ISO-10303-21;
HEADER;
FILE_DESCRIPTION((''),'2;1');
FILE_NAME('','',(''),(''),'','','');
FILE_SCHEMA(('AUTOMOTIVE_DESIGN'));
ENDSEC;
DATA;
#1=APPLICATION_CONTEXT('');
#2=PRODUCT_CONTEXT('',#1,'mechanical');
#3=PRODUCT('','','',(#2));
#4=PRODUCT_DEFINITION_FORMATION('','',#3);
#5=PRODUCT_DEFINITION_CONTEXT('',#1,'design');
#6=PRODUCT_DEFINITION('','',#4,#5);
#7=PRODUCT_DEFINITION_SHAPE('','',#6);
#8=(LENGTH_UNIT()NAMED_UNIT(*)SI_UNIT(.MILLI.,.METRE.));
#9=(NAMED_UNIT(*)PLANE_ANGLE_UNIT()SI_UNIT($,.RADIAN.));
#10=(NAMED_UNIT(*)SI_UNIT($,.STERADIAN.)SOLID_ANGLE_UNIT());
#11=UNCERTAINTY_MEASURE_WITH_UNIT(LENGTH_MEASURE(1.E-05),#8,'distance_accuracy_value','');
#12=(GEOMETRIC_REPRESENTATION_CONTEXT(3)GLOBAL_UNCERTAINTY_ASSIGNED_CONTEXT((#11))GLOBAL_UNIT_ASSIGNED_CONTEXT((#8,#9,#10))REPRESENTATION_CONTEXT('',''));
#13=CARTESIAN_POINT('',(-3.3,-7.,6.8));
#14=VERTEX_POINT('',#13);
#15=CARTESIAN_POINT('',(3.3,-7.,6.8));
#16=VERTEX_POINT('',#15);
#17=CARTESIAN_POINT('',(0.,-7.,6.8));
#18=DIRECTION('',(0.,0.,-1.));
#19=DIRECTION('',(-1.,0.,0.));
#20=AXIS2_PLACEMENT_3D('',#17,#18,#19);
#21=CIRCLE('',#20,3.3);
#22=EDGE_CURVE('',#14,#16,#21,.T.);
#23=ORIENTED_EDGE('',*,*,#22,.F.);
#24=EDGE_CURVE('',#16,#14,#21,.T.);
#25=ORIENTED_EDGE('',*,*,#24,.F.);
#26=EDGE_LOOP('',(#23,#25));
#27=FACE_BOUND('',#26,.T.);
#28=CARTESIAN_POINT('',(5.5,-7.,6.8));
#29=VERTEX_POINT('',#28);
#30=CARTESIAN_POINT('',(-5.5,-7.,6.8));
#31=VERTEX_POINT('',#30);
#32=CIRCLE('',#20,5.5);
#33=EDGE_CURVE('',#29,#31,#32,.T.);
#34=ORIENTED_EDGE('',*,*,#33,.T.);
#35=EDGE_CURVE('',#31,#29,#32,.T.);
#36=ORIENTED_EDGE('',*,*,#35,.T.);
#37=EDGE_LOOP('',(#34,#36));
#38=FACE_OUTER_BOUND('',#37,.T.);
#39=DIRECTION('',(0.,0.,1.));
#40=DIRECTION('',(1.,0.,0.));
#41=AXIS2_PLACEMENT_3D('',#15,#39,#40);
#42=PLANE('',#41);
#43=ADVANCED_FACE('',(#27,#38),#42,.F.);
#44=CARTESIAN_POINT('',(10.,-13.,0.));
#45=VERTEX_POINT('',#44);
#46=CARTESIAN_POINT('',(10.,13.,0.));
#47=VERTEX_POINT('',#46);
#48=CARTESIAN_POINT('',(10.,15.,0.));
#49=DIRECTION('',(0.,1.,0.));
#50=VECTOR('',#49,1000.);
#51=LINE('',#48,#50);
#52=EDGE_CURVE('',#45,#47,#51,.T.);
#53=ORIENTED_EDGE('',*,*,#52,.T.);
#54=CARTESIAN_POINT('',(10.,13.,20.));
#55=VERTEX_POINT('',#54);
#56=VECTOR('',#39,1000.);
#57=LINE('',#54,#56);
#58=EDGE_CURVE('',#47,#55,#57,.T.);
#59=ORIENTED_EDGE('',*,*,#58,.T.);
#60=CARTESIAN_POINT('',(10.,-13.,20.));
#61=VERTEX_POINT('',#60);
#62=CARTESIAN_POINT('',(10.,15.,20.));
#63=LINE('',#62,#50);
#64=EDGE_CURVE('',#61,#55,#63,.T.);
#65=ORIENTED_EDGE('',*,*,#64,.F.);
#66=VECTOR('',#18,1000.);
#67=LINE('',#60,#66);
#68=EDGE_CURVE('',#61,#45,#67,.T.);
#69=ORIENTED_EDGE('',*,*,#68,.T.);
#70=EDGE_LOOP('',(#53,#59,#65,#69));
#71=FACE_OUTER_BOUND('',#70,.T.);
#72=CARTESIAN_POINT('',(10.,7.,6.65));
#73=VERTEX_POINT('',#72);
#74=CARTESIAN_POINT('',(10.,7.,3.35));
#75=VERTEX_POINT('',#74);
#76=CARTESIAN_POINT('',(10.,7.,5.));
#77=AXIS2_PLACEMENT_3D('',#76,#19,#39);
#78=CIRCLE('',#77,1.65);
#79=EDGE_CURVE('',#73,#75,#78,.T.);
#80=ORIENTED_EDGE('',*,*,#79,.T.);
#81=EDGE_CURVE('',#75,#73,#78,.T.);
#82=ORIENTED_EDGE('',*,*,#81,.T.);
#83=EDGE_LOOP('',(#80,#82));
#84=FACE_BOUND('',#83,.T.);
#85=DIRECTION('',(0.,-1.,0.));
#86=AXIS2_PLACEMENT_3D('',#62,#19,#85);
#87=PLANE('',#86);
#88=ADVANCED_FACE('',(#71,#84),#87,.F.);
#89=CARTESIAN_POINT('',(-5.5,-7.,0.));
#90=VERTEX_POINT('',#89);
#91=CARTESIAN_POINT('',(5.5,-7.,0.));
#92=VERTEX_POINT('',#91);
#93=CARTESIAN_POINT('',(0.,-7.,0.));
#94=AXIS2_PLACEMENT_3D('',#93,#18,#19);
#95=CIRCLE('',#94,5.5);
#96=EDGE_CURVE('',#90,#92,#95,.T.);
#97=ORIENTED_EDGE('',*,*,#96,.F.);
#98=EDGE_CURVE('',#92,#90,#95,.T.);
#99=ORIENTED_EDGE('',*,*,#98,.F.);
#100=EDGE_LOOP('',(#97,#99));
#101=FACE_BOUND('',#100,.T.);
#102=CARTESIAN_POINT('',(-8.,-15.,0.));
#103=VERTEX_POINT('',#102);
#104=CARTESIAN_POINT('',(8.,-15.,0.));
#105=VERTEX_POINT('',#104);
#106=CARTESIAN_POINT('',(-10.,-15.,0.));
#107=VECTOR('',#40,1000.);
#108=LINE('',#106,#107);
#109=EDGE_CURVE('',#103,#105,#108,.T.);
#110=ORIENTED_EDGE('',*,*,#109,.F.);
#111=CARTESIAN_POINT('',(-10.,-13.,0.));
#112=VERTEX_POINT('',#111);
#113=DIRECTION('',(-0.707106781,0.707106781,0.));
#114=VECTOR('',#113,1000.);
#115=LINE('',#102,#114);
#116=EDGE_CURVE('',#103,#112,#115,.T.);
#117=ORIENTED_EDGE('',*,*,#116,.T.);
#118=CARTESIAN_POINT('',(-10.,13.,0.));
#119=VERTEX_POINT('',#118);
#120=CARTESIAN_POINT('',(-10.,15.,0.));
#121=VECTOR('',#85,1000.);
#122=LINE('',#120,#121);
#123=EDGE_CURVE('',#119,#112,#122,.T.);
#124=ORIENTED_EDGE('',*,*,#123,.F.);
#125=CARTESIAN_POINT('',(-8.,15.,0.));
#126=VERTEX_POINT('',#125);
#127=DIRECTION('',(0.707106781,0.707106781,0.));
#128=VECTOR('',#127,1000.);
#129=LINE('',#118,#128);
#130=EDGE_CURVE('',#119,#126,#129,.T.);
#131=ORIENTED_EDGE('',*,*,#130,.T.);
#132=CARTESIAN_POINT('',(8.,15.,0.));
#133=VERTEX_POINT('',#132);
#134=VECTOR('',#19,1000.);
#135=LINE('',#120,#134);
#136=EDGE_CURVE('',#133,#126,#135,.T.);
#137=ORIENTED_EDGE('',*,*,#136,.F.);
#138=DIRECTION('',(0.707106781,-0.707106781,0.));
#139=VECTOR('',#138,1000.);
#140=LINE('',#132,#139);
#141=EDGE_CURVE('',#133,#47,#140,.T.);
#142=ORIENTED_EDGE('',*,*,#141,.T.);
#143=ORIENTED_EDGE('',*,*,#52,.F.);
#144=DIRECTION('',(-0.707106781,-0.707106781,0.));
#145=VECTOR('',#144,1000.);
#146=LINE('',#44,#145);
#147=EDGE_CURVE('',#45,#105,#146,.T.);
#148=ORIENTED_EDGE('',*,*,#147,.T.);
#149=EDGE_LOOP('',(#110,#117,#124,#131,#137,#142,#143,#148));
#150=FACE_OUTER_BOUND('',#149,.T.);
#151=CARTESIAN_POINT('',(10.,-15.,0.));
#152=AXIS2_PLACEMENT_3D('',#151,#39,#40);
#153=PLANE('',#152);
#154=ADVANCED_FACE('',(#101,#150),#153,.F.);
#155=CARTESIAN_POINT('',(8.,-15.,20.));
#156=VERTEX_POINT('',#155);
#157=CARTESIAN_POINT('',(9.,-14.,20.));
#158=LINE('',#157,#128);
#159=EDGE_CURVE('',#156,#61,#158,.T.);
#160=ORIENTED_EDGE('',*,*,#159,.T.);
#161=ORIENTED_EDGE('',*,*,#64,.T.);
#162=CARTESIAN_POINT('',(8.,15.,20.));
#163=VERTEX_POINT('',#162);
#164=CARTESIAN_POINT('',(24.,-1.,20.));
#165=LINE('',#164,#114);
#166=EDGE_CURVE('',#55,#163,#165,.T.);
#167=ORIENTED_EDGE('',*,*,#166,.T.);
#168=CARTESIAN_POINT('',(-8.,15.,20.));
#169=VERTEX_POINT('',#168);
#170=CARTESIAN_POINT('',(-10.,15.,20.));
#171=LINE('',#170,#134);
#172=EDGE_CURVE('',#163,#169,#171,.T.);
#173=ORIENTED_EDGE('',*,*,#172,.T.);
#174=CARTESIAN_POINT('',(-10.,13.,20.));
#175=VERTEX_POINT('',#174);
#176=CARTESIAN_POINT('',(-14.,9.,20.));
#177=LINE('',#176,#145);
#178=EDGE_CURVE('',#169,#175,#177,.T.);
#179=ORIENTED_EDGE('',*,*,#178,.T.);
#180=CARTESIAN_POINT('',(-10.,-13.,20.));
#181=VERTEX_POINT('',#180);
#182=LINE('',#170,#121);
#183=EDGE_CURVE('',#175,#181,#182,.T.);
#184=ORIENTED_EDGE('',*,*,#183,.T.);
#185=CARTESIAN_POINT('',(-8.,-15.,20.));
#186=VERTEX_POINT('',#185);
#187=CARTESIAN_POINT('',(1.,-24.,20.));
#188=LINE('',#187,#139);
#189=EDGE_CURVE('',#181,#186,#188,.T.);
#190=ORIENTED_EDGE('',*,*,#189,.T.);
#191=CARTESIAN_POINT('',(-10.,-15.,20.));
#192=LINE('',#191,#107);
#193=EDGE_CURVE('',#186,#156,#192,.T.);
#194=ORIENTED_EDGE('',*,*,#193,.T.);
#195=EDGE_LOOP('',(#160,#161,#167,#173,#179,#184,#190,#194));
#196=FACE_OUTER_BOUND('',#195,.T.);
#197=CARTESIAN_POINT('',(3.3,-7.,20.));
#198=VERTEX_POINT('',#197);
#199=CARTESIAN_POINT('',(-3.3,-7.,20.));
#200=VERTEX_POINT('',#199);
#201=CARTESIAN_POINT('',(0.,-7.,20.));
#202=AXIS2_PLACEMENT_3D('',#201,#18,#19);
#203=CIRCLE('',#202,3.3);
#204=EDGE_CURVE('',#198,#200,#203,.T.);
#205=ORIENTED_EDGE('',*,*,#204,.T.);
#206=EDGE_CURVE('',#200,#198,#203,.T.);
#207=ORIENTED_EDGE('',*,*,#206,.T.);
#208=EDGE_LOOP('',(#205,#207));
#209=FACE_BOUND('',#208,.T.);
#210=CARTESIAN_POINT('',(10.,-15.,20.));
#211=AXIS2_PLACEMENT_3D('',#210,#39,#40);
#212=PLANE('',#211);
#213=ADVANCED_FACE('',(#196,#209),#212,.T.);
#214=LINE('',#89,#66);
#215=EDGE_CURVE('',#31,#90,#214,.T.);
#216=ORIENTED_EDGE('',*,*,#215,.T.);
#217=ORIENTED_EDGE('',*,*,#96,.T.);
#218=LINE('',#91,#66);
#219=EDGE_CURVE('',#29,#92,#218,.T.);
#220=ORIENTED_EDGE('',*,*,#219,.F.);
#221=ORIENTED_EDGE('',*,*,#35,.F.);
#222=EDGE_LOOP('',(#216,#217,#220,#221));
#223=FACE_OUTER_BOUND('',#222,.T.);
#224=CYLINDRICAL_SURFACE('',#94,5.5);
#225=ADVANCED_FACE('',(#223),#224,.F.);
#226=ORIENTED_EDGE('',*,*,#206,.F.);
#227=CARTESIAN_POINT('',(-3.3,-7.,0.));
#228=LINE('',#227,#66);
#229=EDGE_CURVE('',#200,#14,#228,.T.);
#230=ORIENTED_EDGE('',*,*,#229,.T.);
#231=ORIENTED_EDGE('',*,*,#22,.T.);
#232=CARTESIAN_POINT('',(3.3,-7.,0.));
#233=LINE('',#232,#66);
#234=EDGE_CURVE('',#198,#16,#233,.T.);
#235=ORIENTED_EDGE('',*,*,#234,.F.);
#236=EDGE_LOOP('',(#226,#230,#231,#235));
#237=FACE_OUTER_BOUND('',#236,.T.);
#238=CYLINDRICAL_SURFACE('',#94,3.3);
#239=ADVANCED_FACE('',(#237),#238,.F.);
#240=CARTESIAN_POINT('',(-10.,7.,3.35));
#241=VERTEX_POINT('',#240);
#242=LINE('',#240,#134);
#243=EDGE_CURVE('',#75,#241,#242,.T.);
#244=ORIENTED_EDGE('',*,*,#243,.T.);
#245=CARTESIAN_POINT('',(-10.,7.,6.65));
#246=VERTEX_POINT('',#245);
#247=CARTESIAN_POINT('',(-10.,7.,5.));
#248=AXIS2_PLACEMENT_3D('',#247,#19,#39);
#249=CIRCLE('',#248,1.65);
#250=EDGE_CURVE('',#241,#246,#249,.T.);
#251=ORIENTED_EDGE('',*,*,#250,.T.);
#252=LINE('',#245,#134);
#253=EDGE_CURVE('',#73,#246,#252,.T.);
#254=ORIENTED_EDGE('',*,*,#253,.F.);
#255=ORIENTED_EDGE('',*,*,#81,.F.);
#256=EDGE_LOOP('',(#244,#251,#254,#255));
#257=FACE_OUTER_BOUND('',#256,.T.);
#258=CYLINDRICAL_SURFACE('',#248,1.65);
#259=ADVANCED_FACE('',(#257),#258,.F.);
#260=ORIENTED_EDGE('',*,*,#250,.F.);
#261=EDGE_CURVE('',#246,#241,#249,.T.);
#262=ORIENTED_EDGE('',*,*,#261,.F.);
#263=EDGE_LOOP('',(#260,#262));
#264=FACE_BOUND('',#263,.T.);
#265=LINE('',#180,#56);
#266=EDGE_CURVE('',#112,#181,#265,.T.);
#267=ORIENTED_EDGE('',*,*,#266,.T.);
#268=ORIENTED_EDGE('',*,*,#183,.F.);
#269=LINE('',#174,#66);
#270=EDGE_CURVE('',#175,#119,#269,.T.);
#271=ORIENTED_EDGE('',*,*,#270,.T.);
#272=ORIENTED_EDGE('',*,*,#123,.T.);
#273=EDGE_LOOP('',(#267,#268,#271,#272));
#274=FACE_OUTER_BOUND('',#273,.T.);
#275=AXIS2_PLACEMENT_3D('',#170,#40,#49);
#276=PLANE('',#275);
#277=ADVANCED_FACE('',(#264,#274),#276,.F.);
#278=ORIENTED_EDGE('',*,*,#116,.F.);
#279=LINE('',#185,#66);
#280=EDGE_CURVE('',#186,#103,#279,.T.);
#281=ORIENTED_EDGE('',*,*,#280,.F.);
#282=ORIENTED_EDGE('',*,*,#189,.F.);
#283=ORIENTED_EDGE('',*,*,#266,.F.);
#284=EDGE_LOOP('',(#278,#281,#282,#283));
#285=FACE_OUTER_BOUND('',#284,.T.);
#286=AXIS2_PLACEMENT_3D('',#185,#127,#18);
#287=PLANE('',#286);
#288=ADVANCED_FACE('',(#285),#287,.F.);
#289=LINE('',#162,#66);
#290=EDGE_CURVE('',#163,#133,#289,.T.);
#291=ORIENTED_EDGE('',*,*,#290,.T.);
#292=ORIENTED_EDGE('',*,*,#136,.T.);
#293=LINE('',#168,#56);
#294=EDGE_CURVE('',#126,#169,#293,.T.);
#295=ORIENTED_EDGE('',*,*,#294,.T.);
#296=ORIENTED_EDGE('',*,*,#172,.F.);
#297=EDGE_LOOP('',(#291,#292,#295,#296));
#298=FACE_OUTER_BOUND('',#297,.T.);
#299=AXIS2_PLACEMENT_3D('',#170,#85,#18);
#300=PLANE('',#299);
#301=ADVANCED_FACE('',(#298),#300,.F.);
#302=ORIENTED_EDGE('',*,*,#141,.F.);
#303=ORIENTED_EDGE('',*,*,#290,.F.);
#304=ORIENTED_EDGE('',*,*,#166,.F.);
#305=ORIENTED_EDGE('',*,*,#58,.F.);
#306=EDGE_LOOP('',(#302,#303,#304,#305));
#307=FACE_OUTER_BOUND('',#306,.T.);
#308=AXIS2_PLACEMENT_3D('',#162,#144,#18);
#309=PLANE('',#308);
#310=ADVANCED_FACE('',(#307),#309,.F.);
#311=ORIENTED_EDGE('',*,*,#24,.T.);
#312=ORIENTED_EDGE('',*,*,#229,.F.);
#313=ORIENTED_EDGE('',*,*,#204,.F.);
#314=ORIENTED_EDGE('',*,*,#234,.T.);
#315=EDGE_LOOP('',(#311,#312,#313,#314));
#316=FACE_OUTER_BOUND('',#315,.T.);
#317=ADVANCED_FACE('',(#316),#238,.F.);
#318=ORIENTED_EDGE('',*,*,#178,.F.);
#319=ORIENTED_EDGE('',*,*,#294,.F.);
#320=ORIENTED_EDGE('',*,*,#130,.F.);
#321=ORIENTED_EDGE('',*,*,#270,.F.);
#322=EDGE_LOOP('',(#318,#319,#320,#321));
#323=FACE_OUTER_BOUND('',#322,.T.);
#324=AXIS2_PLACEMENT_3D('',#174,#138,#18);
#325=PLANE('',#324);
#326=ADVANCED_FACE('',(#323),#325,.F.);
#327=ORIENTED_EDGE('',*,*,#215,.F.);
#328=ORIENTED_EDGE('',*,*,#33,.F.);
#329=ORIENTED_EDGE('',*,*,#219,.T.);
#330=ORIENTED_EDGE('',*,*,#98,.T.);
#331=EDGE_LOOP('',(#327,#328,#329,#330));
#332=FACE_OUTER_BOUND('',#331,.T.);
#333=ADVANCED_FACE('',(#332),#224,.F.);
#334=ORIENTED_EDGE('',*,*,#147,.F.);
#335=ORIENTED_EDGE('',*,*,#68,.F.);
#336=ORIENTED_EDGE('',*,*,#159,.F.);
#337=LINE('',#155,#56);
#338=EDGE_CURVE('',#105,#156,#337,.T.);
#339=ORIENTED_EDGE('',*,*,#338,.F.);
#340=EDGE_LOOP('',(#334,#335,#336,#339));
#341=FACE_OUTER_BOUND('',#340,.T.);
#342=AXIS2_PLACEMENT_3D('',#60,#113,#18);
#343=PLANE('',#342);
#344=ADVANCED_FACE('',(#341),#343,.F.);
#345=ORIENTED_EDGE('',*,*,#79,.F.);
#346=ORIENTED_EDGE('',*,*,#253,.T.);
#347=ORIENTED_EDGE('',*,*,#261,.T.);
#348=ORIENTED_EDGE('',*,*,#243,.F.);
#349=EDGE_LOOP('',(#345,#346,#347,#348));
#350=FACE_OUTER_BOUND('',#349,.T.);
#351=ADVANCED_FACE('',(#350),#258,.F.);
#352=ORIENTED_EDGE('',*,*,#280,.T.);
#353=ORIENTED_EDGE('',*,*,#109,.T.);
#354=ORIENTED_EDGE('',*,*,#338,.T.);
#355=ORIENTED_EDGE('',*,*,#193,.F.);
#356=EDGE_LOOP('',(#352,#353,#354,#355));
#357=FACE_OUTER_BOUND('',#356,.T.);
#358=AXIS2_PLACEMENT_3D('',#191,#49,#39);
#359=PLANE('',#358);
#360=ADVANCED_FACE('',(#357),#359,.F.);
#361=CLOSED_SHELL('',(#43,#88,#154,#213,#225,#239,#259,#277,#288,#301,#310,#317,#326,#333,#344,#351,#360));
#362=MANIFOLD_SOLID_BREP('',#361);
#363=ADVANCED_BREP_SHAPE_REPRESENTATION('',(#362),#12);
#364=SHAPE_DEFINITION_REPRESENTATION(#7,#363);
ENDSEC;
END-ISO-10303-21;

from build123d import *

# Parameters (mm, degrees)
SKETCH_1_W                = 20
SKETCH_1_H                = 30
EXTRUDE_1_DEPTH           = 20
HOLE_WIZARD_1_D           = 6.6
HOLE_WIZARD_1_CBORE_D     = 11
HOLE_WIZARD_1_CBORE_DEPTH = 6.8
HOLE_WIZARD_M4_1_D        = 3.3
CHAMFER_1_SIZE            = 2


with BuildPart() as part:
    # 草图1 → 凸台-拉伸1 (new body)
    with BuildSketch(Plane.XY):
        Rectangle(SKETCH_1_W, SKETCH_1_H)
    extrude(amount=EXTRUDE_1_DEPTH)

    # 打孔尺寸根据内六角圆柱头螺钉的类型1 (through all)
    with Locations(Plane(origin=(3.133596483, 10.907898158, 0), x_dir=(1, 0, 0), z_dir=(0, 0, -1))):
        with Locations((-3.133596483, 17.907898158)):
            CounterBoreHole(HOLE_WIZARD_1_D / 2, HOLE_WIZARD_1_CBORE_D / 2, HOLE_WIZARD_1_CBORE_DEPTH)

    # M4 螺纹孔1 (through all)
    with Locations(Plane.ZY.offset(10)):
        with Locations((5, 7)):
            Hole(HOLE_WIZARD_M4_1_D / 2)

    # 倒角1
    chamfer_1_edges = [part.edges().sort_by_distance(p)[0] for p in [
        (10, -15, 10),
        (-10, -15, 10),
        (-10, 15, 10),
        (10, 15, 10),
    ]]
    chamfer(chamfer_1_edges, length=CHAMFER_1_SIZE)


solid = part.part
